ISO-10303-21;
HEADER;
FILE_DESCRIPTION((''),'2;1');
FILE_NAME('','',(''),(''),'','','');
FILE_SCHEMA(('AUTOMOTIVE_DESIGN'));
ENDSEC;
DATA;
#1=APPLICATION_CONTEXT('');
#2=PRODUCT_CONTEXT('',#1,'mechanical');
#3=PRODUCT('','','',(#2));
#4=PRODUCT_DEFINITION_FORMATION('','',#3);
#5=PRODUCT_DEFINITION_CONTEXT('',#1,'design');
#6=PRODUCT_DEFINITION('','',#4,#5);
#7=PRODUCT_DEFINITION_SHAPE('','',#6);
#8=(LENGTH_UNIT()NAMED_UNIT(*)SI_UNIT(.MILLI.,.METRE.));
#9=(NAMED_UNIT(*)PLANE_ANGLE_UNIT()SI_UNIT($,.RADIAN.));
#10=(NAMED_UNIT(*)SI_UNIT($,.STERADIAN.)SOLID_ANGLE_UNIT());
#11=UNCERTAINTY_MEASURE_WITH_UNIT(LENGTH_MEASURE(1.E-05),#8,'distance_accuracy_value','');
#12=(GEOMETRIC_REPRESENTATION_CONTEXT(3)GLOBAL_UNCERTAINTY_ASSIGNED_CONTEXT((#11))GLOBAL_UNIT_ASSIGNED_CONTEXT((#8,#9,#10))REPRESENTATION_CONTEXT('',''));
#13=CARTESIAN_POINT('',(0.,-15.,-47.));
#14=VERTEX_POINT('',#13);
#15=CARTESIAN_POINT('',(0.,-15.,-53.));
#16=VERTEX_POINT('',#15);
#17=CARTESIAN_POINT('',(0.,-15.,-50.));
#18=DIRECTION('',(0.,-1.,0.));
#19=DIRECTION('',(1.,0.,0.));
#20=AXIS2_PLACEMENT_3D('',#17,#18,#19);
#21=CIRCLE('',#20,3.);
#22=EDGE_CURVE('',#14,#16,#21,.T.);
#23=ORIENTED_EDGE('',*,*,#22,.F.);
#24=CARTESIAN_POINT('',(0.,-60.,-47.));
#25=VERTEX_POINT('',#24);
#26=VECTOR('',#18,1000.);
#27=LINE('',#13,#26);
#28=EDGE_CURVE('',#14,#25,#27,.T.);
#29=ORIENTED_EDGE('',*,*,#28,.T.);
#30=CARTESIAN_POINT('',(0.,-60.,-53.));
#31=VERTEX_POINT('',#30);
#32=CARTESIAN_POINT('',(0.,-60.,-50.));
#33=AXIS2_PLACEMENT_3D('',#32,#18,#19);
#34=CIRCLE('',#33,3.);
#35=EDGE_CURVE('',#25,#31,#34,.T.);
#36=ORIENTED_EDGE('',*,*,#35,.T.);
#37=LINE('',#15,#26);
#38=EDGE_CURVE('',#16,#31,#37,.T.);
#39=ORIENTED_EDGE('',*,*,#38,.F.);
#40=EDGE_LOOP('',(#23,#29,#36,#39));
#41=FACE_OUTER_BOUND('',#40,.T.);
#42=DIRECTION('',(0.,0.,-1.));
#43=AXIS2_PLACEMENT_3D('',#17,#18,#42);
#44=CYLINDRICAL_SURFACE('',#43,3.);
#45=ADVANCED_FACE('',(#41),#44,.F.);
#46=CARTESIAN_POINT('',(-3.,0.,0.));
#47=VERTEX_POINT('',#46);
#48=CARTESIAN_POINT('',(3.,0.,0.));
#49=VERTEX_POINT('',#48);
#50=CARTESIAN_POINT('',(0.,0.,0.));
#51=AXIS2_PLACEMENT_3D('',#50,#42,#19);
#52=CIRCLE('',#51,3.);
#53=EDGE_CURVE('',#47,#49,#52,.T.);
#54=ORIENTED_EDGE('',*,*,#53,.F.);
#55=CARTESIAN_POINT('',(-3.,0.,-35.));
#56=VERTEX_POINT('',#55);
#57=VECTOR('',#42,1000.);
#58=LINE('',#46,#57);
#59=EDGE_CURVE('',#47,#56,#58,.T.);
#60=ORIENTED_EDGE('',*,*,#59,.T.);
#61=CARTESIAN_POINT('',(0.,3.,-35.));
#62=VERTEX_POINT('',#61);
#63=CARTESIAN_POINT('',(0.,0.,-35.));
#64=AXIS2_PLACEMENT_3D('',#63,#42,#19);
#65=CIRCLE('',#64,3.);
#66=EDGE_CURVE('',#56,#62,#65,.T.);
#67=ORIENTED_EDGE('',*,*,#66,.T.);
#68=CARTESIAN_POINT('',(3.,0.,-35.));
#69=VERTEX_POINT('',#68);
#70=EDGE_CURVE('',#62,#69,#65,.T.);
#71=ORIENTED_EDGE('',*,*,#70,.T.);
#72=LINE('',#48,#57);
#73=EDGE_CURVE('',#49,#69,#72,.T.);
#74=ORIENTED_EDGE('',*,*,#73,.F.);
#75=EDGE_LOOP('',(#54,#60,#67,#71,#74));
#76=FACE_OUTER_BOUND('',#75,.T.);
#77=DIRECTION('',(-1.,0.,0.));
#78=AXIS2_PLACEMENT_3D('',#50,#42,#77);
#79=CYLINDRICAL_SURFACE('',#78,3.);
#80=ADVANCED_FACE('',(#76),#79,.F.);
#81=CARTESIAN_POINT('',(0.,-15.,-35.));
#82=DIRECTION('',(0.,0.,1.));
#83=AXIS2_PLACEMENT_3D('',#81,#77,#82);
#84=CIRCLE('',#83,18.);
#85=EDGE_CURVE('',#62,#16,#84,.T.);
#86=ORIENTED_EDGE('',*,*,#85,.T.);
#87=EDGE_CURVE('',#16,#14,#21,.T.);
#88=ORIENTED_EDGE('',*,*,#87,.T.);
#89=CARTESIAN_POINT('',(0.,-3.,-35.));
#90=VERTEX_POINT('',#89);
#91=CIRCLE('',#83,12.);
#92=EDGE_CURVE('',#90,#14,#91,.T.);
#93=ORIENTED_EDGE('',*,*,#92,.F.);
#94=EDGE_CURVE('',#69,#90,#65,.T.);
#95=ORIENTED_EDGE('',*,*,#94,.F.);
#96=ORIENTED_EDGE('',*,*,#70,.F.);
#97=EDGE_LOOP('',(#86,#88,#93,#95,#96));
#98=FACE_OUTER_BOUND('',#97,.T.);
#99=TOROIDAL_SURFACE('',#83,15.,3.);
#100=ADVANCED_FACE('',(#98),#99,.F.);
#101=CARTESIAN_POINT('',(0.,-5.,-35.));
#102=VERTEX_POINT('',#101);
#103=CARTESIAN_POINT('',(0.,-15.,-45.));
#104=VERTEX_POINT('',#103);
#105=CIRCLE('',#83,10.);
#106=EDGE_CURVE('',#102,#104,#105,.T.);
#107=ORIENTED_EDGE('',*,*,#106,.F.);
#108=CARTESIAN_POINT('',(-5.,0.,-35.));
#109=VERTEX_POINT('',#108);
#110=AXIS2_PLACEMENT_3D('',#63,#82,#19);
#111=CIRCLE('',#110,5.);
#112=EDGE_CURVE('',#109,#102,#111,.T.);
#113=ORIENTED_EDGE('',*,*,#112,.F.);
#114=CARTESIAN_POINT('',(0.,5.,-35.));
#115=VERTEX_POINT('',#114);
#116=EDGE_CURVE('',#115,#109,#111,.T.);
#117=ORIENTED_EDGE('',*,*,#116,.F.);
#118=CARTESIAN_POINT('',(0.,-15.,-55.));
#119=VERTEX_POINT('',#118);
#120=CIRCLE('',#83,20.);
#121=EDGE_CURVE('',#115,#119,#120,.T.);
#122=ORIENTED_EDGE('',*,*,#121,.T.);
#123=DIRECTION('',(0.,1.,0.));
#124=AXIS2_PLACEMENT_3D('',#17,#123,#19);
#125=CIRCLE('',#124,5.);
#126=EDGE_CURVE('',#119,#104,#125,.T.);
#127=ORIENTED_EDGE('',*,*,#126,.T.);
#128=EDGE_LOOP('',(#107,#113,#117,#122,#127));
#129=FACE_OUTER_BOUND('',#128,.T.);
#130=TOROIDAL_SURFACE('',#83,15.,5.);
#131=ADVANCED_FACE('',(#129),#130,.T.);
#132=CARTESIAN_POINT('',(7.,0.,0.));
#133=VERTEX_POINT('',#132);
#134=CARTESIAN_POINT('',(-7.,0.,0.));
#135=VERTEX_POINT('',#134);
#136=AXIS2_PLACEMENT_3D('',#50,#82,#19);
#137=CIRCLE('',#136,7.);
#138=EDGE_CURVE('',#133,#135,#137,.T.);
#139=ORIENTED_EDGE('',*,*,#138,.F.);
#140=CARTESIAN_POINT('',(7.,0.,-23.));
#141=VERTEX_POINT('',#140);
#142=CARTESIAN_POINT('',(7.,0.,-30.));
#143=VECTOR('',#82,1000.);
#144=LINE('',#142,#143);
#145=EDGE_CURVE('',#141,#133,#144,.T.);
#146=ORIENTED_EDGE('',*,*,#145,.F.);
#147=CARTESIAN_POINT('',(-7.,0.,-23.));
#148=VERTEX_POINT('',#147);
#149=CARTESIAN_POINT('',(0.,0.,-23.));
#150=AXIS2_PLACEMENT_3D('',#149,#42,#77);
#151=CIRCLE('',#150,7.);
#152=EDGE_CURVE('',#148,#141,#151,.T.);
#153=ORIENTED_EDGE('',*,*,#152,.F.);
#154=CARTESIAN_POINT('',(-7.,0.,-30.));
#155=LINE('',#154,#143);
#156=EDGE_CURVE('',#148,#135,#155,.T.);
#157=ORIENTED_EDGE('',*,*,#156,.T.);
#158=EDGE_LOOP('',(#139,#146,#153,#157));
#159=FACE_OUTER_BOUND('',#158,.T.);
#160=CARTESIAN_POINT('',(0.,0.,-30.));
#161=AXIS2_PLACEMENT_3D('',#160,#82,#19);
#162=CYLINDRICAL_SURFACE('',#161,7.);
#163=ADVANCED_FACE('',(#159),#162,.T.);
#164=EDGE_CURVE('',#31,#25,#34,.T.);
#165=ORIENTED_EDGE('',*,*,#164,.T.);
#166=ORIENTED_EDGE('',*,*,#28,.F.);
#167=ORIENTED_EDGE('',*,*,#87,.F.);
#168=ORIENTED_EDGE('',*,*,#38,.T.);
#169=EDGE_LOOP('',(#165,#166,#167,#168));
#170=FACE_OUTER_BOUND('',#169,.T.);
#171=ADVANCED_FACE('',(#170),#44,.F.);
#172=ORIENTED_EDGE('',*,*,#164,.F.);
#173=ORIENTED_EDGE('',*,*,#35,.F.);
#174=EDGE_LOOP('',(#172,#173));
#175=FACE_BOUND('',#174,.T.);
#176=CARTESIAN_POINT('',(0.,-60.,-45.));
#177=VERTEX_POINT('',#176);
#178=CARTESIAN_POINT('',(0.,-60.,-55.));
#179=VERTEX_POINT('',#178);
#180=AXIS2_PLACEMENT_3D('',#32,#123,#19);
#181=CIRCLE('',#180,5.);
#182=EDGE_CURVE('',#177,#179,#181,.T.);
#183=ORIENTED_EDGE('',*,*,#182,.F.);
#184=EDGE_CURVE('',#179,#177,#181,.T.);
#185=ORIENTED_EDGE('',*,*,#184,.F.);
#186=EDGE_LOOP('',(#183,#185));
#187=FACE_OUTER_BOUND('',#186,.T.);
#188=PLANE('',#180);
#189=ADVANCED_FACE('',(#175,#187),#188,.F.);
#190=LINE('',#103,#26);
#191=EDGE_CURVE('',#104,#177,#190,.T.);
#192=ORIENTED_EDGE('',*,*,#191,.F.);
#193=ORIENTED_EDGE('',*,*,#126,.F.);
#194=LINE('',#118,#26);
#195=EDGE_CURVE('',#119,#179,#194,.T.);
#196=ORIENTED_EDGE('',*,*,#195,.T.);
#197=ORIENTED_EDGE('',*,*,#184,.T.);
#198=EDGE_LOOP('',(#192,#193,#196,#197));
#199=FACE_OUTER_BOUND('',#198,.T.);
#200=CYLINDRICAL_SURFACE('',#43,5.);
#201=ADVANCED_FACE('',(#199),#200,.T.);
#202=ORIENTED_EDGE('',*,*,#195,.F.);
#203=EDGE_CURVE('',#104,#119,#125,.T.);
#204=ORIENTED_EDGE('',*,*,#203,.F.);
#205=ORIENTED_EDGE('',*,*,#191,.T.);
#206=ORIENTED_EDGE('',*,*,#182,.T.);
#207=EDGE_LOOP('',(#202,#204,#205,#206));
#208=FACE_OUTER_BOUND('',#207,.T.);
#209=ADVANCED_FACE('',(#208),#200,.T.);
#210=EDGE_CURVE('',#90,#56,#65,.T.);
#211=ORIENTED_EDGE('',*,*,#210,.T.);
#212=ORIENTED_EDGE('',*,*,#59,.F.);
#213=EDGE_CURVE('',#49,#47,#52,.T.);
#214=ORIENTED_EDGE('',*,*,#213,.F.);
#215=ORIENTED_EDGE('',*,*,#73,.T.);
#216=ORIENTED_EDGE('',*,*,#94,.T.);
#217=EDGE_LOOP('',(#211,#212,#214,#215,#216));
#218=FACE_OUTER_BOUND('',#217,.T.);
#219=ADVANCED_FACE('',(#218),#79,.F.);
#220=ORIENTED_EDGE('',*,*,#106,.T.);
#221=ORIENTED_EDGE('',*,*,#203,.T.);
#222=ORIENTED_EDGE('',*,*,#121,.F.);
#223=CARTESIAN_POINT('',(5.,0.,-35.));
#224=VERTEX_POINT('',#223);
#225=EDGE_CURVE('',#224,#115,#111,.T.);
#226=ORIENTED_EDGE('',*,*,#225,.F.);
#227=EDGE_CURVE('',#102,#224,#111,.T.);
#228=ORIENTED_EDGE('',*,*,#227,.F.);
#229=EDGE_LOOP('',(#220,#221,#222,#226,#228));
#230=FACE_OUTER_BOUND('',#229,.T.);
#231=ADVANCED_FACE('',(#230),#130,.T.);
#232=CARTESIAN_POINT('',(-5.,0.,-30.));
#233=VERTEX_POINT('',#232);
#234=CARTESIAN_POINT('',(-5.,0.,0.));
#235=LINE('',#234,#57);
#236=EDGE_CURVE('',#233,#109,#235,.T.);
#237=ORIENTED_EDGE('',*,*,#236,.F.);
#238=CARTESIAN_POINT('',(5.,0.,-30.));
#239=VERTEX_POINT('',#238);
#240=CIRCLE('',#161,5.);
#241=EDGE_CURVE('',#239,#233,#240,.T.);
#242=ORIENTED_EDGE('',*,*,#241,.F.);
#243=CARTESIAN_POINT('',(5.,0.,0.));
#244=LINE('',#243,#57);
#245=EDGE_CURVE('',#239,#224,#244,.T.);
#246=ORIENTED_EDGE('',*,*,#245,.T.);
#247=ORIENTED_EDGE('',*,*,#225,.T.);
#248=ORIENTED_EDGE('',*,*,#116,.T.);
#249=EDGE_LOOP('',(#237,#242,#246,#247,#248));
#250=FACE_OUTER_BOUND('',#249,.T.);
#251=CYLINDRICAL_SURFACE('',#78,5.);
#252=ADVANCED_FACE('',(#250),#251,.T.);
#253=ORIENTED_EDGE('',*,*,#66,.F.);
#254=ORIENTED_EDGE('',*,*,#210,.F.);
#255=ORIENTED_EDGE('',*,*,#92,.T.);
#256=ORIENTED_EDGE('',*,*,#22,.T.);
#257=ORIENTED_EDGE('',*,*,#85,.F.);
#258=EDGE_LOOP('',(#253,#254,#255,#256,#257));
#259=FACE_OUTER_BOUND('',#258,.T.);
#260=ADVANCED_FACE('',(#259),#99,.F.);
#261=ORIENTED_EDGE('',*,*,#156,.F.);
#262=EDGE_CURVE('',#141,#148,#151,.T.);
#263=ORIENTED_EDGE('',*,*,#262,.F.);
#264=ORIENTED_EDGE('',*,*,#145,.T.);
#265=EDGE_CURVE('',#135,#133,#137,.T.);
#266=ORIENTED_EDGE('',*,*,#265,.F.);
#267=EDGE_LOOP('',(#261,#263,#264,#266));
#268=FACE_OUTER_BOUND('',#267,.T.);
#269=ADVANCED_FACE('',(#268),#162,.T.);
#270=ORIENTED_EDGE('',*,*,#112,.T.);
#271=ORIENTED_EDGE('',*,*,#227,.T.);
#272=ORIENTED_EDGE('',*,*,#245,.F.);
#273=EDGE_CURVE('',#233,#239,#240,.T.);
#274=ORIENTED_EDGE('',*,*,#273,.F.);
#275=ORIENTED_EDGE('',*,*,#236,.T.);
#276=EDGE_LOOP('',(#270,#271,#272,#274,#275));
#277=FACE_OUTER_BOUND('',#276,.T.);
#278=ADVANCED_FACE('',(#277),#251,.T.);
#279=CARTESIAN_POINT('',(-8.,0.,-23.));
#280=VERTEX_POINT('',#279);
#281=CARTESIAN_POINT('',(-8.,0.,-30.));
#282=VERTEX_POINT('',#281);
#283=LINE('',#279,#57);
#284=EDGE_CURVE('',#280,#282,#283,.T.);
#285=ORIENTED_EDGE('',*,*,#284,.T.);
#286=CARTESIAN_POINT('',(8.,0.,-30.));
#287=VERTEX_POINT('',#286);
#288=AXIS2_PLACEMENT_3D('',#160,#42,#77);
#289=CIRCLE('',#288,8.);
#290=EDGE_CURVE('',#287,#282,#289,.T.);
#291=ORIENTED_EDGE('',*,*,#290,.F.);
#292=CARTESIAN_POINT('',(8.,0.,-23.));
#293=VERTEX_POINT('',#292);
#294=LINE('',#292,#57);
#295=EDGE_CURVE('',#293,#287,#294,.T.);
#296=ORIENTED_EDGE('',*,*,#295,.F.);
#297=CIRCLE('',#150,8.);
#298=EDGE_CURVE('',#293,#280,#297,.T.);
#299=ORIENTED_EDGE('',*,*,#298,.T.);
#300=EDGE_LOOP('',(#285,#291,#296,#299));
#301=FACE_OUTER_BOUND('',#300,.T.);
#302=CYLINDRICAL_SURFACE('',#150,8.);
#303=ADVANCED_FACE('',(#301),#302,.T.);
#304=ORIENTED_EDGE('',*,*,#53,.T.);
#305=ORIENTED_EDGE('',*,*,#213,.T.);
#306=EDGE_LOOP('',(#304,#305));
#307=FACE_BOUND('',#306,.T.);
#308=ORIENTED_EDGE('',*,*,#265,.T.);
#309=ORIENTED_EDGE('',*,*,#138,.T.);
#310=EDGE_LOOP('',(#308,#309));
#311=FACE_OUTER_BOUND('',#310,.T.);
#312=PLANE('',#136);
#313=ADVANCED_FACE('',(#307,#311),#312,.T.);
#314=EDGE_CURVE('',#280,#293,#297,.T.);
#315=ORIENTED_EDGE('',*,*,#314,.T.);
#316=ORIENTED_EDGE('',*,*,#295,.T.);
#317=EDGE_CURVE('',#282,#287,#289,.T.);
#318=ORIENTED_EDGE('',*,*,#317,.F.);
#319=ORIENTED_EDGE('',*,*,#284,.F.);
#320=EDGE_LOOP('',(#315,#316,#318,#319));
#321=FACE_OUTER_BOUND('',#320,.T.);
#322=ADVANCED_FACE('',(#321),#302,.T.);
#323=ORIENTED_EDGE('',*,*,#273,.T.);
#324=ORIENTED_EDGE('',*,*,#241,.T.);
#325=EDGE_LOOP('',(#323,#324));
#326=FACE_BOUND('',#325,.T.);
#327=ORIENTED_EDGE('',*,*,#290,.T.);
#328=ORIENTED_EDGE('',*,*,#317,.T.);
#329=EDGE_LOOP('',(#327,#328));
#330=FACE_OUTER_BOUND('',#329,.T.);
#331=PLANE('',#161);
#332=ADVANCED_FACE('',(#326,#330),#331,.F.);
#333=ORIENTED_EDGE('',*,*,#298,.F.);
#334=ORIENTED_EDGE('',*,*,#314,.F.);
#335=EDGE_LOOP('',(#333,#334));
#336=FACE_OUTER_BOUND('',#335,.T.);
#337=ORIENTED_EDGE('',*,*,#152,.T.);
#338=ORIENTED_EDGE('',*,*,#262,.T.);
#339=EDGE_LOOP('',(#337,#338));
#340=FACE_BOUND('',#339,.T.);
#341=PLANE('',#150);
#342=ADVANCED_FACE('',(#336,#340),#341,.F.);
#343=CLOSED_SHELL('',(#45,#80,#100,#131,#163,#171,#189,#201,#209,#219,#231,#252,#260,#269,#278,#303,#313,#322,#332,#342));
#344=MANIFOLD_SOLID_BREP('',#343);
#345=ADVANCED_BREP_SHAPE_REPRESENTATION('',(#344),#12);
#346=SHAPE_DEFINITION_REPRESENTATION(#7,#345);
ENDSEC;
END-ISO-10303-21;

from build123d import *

# Parameters (mm, degrees)
SKETCH2_R           = 5
SKETCH2_R_2         = 3
BOSS_EXTRUDE1_START = -30
SKETCH3_R           = 7
SKETCH3_R_2         = 5
BOSS_EXTRUDE1_DEPTH = 30
SKETCH4_R           = 8
SKETCH4_R_2         = 7
BOSS_EXTRUDE2_DEPTH = 7


with BuildPart() as part:
    # Sweep1: sweep along a path in Sketch1
    with BuildLine(Plane(origin=(0, 0, 0), x_dir=(0, 0, -1), z_dir=(1, 0, 0))) as sweep1_path:
        Line((0, 0), (35, 0))
        ThreePointArc((35, 0), (45.606601718, -4.393398282), (50, -15))
        Line((50, -15), (50, -60))
    # Sketch2 → Sweep1 (sweep)
    with BuildSketch(Plane.XY):
        Circle(SKETCH2_R)
        Circle(SKETCH2_R_2, mode=Mode.SUBTRACT)
    sweep(path=sweep1_path.line)

    # Sketch3 → Boss-Extrude1 (add)
    with BuildSketch(Plane.XY.offset(BOSS_EXTRUDE1_START)):
        Circle(SKETCH3_R)
        with Locations(Location((0, 0, 0), (0, 0, 90))):
            Circle(SKETCH3_R_2, mode=Mode.SUBTRACT)
    extrude(amount=BOSS_EXTRUDE1_DEPTH)

    # Sketch4 → Boss-Extrude2 (add)
    with BuildSketch(Plane(origin=(0, 0, -30), x_dir=(-1, 0, 0), z_dir=(0, 0, -1))):
        Circle(SKETCH4_R)
        with Locations(Location((0, 0, 0), (0, 0, 180))):
            Circle(SKETCH4_R_2, mode=Mode.SUBTRACT)
    extrude(amount=-BOSS_EXTRUDE2_DEPTH)


solid = part.part
